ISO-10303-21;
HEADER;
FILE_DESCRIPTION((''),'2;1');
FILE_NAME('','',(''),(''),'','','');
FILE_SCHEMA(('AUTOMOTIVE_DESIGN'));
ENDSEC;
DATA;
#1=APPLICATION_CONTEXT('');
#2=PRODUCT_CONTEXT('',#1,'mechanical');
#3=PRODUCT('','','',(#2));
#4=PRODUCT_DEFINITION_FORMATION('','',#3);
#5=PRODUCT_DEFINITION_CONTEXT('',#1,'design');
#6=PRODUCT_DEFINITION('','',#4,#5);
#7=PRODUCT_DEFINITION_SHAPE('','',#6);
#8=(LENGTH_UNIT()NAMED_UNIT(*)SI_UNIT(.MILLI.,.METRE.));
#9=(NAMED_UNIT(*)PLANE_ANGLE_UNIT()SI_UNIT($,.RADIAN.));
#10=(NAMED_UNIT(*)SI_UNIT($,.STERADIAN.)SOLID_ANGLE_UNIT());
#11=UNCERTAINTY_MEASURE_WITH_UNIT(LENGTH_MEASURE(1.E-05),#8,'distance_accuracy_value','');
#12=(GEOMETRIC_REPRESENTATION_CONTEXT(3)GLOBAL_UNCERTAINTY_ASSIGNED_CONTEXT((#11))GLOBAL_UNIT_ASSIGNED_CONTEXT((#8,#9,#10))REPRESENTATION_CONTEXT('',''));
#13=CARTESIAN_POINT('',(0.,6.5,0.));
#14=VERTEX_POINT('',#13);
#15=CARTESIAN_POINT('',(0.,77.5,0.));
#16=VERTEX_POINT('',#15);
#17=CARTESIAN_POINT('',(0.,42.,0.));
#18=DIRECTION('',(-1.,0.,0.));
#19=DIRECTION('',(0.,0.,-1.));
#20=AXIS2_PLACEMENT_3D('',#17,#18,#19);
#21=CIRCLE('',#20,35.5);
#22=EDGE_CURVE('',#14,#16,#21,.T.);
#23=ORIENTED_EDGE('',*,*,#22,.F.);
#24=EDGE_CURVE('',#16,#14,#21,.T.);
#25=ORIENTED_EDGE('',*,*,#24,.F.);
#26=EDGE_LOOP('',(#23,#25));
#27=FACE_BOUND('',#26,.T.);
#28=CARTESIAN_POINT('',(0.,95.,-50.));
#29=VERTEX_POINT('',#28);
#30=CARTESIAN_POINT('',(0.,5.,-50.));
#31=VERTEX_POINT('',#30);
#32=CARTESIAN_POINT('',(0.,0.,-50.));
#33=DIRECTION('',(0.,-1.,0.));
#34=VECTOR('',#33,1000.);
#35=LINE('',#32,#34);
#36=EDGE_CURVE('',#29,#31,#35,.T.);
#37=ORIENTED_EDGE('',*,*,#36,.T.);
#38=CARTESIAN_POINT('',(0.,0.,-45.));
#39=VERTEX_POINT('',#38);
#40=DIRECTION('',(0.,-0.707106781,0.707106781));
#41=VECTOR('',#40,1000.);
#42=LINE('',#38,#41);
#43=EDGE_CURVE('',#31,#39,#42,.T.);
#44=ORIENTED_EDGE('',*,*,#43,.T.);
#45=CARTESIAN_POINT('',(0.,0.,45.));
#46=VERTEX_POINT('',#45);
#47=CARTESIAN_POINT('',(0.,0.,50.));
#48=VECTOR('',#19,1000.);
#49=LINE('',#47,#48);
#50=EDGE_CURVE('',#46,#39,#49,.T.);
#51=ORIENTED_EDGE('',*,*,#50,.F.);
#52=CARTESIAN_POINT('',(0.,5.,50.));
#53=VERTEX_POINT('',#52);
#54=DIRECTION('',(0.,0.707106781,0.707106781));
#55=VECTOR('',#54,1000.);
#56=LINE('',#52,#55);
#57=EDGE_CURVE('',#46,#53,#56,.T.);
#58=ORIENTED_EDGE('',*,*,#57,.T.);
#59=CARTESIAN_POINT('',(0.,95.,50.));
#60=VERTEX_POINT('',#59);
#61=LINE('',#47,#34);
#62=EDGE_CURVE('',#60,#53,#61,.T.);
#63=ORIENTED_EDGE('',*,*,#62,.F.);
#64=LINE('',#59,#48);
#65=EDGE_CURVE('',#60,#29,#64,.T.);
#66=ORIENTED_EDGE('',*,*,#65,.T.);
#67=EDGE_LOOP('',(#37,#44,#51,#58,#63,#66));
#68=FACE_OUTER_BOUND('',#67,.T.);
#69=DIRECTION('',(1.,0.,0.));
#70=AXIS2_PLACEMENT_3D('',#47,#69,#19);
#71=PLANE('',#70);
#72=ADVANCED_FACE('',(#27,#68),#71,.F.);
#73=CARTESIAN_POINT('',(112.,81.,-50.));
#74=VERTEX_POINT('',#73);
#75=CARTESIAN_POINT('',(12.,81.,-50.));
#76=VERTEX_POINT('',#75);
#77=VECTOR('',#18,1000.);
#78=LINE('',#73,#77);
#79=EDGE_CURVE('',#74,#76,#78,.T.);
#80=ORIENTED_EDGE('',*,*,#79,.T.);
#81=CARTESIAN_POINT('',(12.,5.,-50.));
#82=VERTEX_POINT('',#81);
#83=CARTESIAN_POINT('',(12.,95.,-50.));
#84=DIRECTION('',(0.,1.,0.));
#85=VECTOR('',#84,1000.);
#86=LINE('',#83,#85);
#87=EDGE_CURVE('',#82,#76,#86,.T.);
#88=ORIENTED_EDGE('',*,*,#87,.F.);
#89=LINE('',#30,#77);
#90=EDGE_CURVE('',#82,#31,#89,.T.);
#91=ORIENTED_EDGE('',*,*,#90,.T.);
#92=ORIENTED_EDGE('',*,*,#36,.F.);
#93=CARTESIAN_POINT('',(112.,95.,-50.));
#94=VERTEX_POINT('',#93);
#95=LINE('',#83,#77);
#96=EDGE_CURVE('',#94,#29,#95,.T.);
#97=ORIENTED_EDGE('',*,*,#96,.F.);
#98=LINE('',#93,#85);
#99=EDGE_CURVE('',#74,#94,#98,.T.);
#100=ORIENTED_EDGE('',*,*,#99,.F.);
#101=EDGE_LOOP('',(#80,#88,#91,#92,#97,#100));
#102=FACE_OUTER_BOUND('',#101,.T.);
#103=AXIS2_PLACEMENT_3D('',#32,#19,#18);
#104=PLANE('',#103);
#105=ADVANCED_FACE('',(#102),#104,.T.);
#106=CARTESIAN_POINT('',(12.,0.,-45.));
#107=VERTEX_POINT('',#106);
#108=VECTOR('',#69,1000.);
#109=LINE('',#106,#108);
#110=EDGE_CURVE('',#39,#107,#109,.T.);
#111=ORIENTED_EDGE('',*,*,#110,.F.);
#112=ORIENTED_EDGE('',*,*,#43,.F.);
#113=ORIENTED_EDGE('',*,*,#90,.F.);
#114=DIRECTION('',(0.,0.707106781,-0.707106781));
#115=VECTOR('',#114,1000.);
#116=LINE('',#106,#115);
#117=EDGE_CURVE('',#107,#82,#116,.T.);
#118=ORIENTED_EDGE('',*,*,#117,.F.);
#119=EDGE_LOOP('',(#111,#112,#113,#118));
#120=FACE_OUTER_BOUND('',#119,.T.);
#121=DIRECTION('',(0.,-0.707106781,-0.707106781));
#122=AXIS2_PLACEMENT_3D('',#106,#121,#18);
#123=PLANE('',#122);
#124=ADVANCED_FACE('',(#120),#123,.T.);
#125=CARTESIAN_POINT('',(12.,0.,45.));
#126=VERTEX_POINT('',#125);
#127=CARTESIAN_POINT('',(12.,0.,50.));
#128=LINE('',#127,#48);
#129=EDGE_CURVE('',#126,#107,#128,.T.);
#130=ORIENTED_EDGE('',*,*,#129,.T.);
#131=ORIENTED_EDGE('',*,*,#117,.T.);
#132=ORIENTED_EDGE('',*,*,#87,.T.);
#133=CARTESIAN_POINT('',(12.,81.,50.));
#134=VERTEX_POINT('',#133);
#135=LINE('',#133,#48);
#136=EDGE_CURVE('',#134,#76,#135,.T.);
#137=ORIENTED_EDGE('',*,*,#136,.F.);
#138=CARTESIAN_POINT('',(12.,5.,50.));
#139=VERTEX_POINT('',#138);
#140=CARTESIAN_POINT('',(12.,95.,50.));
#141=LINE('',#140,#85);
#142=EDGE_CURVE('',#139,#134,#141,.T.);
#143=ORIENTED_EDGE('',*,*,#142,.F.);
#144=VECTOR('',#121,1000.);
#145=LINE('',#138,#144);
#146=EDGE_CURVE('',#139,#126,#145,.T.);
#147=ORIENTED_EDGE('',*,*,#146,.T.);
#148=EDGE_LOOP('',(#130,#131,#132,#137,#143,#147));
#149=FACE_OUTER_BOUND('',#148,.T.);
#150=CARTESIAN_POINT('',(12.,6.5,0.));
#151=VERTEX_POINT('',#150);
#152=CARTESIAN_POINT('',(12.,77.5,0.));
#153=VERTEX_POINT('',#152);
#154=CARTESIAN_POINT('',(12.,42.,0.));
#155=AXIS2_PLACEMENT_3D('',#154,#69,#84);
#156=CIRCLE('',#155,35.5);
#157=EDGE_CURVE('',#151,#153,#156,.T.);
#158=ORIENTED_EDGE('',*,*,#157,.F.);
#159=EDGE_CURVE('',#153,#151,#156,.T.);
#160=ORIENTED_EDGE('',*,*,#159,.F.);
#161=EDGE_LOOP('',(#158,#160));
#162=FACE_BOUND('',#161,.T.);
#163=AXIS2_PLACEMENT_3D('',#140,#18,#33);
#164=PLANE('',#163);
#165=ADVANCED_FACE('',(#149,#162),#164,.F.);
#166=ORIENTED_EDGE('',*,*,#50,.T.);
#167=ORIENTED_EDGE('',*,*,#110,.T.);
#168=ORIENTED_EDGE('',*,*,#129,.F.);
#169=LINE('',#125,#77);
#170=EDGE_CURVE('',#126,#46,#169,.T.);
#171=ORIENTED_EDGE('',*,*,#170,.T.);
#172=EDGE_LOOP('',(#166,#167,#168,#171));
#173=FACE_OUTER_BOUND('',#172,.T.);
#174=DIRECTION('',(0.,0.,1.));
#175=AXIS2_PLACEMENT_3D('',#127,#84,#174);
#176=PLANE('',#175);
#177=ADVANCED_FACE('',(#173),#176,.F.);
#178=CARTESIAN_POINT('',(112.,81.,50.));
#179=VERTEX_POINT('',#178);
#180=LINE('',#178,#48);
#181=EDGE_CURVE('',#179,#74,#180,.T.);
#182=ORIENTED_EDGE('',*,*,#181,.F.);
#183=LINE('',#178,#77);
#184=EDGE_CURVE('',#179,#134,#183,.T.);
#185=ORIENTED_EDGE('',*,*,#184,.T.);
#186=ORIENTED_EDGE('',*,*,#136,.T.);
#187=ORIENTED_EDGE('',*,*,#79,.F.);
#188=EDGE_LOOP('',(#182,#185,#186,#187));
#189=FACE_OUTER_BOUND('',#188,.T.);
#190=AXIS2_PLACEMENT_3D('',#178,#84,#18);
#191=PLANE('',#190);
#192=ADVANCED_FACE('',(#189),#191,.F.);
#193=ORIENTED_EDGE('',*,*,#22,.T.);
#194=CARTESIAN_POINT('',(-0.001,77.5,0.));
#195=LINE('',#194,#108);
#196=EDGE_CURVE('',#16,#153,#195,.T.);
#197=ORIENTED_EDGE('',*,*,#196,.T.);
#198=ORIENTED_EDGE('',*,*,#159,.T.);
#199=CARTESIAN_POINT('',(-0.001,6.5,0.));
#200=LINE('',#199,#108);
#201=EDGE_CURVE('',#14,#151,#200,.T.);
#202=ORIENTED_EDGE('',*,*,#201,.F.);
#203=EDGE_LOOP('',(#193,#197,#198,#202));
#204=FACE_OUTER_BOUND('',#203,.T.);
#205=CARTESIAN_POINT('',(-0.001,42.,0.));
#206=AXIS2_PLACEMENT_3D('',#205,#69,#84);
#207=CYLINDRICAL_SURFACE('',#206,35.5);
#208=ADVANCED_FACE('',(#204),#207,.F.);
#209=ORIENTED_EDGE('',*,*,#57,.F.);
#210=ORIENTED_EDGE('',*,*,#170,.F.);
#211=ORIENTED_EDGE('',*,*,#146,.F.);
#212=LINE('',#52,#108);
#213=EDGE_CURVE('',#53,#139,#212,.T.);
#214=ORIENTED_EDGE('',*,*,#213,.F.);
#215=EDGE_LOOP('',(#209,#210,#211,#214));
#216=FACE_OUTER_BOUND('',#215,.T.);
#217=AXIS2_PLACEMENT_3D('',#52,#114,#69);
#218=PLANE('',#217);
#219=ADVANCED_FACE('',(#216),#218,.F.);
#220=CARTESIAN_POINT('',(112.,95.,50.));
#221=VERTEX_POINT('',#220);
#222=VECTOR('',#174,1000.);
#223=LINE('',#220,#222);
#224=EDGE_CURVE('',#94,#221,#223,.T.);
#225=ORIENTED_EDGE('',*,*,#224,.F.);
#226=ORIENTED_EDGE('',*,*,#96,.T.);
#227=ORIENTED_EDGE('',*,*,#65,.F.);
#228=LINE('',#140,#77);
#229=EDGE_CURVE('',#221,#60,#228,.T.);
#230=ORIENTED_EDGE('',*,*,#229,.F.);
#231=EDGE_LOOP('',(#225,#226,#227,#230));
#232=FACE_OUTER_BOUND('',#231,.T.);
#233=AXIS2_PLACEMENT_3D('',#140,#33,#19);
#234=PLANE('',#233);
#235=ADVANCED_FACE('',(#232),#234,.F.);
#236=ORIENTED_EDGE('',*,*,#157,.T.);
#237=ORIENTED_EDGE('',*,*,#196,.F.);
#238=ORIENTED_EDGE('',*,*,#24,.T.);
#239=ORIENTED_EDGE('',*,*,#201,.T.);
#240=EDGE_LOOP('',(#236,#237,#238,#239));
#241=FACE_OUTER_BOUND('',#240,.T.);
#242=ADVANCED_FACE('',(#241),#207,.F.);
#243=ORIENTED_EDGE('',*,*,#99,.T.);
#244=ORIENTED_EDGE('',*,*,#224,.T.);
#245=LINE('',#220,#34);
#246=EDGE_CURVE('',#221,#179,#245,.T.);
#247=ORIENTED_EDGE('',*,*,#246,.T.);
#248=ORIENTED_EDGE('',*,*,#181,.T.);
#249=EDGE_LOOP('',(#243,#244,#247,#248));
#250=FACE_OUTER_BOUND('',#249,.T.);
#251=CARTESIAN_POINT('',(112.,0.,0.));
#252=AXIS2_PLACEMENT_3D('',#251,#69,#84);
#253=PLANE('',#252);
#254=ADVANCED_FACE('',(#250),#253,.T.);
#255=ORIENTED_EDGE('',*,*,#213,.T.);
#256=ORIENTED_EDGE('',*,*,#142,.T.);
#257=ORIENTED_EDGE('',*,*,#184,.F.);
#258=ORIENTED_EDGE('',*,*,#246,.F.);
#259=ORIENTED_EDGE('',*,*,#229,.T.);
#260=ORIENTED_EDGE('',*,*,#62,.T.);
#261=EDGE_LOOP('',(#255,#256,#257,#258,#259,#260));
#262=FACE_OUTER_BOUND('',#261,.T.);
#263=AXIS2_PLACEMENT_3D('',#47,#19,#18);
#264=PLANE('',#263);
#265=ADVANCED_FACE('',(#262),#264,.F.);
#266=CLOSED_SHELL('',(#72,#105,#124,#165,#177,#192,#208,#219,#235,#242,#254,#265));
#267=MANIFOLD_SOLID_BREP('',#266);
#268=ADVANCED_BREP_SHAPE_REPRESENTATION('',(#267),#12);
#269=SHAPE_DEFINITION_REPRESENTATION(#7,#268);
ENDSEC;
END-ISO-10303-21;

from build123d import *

# Parameters (mm, degrees)
SKETCH_1_W          = 12
SKETCH_1_H          = 95
EXTRUDE_1_DEPTH     = 50
CUT_EXTRUDE_1_REACH = 110.023
SKETCH_2_R          = 35.5
SKETCH_3_W          = 100
SKETCH_3_H          = 14
EXTRUDE_2_DEPTH     = 100
CHAMFER_1_SIZE      = 5


with BuildPart() as part:
    # 草图1 → 凸台-拉伸1 (new, symmetric)
    with BuildSketch(Plane.XY):
        with Locations((6, 47.5)):
            Rectangle(SKETCH_1_W, SKETCH_1_H)
    extrude(amount=EXTRUDE_1_DEPTH, both=True)

    # 草图2 → 切除-拉伸1 (cut, up to next)
    with BuildSketch(Plane(origin=(12, 0, 0), x_dir=(0, 0, -1), z_dir=(1, 0, 0)), mode=Mode.PRIVATE) as cut_extrude_1_sk1:
        with Locations(Location((0, 42, 0), (0, 0, 90))):
            Circle(SKETCH_2_R)
    cut_extrude_1_tool1 = extrude(cut_extrude_1_sk1.sketch, amount=-CUT_EXTRUDE_1_REACH, mode=Mode.PRIVATE) & part.part
    add(cut_extrude_1_tool1.solids().sort_by_distance((12, 42, 0))[0], mode=Mode.SUBTRACT)

    # 草图3 → 凸台-拉伸2 (add)
    with BuildSketch(Plane(origin=(12, 0, 0), x_dir=(0, 0, -1), z_dir=(1, 0, 0))):
        with Locations((0, 88)):
            Rectangle(SKETCH_3_W, SKETCH_3_H)
    extrude(amount=EXTRUDE_2_DEPTH)

    # 倒角1
    chamfer_1_edges = [part.edges().sort_by_distance(p)[0] for p in [
        (6, 0, 50),
        (6, 0, -50),
    ]]
    chamfer(chamfer_1_edges, length=CHAMFER_1_SIZE)


solid = part.part
